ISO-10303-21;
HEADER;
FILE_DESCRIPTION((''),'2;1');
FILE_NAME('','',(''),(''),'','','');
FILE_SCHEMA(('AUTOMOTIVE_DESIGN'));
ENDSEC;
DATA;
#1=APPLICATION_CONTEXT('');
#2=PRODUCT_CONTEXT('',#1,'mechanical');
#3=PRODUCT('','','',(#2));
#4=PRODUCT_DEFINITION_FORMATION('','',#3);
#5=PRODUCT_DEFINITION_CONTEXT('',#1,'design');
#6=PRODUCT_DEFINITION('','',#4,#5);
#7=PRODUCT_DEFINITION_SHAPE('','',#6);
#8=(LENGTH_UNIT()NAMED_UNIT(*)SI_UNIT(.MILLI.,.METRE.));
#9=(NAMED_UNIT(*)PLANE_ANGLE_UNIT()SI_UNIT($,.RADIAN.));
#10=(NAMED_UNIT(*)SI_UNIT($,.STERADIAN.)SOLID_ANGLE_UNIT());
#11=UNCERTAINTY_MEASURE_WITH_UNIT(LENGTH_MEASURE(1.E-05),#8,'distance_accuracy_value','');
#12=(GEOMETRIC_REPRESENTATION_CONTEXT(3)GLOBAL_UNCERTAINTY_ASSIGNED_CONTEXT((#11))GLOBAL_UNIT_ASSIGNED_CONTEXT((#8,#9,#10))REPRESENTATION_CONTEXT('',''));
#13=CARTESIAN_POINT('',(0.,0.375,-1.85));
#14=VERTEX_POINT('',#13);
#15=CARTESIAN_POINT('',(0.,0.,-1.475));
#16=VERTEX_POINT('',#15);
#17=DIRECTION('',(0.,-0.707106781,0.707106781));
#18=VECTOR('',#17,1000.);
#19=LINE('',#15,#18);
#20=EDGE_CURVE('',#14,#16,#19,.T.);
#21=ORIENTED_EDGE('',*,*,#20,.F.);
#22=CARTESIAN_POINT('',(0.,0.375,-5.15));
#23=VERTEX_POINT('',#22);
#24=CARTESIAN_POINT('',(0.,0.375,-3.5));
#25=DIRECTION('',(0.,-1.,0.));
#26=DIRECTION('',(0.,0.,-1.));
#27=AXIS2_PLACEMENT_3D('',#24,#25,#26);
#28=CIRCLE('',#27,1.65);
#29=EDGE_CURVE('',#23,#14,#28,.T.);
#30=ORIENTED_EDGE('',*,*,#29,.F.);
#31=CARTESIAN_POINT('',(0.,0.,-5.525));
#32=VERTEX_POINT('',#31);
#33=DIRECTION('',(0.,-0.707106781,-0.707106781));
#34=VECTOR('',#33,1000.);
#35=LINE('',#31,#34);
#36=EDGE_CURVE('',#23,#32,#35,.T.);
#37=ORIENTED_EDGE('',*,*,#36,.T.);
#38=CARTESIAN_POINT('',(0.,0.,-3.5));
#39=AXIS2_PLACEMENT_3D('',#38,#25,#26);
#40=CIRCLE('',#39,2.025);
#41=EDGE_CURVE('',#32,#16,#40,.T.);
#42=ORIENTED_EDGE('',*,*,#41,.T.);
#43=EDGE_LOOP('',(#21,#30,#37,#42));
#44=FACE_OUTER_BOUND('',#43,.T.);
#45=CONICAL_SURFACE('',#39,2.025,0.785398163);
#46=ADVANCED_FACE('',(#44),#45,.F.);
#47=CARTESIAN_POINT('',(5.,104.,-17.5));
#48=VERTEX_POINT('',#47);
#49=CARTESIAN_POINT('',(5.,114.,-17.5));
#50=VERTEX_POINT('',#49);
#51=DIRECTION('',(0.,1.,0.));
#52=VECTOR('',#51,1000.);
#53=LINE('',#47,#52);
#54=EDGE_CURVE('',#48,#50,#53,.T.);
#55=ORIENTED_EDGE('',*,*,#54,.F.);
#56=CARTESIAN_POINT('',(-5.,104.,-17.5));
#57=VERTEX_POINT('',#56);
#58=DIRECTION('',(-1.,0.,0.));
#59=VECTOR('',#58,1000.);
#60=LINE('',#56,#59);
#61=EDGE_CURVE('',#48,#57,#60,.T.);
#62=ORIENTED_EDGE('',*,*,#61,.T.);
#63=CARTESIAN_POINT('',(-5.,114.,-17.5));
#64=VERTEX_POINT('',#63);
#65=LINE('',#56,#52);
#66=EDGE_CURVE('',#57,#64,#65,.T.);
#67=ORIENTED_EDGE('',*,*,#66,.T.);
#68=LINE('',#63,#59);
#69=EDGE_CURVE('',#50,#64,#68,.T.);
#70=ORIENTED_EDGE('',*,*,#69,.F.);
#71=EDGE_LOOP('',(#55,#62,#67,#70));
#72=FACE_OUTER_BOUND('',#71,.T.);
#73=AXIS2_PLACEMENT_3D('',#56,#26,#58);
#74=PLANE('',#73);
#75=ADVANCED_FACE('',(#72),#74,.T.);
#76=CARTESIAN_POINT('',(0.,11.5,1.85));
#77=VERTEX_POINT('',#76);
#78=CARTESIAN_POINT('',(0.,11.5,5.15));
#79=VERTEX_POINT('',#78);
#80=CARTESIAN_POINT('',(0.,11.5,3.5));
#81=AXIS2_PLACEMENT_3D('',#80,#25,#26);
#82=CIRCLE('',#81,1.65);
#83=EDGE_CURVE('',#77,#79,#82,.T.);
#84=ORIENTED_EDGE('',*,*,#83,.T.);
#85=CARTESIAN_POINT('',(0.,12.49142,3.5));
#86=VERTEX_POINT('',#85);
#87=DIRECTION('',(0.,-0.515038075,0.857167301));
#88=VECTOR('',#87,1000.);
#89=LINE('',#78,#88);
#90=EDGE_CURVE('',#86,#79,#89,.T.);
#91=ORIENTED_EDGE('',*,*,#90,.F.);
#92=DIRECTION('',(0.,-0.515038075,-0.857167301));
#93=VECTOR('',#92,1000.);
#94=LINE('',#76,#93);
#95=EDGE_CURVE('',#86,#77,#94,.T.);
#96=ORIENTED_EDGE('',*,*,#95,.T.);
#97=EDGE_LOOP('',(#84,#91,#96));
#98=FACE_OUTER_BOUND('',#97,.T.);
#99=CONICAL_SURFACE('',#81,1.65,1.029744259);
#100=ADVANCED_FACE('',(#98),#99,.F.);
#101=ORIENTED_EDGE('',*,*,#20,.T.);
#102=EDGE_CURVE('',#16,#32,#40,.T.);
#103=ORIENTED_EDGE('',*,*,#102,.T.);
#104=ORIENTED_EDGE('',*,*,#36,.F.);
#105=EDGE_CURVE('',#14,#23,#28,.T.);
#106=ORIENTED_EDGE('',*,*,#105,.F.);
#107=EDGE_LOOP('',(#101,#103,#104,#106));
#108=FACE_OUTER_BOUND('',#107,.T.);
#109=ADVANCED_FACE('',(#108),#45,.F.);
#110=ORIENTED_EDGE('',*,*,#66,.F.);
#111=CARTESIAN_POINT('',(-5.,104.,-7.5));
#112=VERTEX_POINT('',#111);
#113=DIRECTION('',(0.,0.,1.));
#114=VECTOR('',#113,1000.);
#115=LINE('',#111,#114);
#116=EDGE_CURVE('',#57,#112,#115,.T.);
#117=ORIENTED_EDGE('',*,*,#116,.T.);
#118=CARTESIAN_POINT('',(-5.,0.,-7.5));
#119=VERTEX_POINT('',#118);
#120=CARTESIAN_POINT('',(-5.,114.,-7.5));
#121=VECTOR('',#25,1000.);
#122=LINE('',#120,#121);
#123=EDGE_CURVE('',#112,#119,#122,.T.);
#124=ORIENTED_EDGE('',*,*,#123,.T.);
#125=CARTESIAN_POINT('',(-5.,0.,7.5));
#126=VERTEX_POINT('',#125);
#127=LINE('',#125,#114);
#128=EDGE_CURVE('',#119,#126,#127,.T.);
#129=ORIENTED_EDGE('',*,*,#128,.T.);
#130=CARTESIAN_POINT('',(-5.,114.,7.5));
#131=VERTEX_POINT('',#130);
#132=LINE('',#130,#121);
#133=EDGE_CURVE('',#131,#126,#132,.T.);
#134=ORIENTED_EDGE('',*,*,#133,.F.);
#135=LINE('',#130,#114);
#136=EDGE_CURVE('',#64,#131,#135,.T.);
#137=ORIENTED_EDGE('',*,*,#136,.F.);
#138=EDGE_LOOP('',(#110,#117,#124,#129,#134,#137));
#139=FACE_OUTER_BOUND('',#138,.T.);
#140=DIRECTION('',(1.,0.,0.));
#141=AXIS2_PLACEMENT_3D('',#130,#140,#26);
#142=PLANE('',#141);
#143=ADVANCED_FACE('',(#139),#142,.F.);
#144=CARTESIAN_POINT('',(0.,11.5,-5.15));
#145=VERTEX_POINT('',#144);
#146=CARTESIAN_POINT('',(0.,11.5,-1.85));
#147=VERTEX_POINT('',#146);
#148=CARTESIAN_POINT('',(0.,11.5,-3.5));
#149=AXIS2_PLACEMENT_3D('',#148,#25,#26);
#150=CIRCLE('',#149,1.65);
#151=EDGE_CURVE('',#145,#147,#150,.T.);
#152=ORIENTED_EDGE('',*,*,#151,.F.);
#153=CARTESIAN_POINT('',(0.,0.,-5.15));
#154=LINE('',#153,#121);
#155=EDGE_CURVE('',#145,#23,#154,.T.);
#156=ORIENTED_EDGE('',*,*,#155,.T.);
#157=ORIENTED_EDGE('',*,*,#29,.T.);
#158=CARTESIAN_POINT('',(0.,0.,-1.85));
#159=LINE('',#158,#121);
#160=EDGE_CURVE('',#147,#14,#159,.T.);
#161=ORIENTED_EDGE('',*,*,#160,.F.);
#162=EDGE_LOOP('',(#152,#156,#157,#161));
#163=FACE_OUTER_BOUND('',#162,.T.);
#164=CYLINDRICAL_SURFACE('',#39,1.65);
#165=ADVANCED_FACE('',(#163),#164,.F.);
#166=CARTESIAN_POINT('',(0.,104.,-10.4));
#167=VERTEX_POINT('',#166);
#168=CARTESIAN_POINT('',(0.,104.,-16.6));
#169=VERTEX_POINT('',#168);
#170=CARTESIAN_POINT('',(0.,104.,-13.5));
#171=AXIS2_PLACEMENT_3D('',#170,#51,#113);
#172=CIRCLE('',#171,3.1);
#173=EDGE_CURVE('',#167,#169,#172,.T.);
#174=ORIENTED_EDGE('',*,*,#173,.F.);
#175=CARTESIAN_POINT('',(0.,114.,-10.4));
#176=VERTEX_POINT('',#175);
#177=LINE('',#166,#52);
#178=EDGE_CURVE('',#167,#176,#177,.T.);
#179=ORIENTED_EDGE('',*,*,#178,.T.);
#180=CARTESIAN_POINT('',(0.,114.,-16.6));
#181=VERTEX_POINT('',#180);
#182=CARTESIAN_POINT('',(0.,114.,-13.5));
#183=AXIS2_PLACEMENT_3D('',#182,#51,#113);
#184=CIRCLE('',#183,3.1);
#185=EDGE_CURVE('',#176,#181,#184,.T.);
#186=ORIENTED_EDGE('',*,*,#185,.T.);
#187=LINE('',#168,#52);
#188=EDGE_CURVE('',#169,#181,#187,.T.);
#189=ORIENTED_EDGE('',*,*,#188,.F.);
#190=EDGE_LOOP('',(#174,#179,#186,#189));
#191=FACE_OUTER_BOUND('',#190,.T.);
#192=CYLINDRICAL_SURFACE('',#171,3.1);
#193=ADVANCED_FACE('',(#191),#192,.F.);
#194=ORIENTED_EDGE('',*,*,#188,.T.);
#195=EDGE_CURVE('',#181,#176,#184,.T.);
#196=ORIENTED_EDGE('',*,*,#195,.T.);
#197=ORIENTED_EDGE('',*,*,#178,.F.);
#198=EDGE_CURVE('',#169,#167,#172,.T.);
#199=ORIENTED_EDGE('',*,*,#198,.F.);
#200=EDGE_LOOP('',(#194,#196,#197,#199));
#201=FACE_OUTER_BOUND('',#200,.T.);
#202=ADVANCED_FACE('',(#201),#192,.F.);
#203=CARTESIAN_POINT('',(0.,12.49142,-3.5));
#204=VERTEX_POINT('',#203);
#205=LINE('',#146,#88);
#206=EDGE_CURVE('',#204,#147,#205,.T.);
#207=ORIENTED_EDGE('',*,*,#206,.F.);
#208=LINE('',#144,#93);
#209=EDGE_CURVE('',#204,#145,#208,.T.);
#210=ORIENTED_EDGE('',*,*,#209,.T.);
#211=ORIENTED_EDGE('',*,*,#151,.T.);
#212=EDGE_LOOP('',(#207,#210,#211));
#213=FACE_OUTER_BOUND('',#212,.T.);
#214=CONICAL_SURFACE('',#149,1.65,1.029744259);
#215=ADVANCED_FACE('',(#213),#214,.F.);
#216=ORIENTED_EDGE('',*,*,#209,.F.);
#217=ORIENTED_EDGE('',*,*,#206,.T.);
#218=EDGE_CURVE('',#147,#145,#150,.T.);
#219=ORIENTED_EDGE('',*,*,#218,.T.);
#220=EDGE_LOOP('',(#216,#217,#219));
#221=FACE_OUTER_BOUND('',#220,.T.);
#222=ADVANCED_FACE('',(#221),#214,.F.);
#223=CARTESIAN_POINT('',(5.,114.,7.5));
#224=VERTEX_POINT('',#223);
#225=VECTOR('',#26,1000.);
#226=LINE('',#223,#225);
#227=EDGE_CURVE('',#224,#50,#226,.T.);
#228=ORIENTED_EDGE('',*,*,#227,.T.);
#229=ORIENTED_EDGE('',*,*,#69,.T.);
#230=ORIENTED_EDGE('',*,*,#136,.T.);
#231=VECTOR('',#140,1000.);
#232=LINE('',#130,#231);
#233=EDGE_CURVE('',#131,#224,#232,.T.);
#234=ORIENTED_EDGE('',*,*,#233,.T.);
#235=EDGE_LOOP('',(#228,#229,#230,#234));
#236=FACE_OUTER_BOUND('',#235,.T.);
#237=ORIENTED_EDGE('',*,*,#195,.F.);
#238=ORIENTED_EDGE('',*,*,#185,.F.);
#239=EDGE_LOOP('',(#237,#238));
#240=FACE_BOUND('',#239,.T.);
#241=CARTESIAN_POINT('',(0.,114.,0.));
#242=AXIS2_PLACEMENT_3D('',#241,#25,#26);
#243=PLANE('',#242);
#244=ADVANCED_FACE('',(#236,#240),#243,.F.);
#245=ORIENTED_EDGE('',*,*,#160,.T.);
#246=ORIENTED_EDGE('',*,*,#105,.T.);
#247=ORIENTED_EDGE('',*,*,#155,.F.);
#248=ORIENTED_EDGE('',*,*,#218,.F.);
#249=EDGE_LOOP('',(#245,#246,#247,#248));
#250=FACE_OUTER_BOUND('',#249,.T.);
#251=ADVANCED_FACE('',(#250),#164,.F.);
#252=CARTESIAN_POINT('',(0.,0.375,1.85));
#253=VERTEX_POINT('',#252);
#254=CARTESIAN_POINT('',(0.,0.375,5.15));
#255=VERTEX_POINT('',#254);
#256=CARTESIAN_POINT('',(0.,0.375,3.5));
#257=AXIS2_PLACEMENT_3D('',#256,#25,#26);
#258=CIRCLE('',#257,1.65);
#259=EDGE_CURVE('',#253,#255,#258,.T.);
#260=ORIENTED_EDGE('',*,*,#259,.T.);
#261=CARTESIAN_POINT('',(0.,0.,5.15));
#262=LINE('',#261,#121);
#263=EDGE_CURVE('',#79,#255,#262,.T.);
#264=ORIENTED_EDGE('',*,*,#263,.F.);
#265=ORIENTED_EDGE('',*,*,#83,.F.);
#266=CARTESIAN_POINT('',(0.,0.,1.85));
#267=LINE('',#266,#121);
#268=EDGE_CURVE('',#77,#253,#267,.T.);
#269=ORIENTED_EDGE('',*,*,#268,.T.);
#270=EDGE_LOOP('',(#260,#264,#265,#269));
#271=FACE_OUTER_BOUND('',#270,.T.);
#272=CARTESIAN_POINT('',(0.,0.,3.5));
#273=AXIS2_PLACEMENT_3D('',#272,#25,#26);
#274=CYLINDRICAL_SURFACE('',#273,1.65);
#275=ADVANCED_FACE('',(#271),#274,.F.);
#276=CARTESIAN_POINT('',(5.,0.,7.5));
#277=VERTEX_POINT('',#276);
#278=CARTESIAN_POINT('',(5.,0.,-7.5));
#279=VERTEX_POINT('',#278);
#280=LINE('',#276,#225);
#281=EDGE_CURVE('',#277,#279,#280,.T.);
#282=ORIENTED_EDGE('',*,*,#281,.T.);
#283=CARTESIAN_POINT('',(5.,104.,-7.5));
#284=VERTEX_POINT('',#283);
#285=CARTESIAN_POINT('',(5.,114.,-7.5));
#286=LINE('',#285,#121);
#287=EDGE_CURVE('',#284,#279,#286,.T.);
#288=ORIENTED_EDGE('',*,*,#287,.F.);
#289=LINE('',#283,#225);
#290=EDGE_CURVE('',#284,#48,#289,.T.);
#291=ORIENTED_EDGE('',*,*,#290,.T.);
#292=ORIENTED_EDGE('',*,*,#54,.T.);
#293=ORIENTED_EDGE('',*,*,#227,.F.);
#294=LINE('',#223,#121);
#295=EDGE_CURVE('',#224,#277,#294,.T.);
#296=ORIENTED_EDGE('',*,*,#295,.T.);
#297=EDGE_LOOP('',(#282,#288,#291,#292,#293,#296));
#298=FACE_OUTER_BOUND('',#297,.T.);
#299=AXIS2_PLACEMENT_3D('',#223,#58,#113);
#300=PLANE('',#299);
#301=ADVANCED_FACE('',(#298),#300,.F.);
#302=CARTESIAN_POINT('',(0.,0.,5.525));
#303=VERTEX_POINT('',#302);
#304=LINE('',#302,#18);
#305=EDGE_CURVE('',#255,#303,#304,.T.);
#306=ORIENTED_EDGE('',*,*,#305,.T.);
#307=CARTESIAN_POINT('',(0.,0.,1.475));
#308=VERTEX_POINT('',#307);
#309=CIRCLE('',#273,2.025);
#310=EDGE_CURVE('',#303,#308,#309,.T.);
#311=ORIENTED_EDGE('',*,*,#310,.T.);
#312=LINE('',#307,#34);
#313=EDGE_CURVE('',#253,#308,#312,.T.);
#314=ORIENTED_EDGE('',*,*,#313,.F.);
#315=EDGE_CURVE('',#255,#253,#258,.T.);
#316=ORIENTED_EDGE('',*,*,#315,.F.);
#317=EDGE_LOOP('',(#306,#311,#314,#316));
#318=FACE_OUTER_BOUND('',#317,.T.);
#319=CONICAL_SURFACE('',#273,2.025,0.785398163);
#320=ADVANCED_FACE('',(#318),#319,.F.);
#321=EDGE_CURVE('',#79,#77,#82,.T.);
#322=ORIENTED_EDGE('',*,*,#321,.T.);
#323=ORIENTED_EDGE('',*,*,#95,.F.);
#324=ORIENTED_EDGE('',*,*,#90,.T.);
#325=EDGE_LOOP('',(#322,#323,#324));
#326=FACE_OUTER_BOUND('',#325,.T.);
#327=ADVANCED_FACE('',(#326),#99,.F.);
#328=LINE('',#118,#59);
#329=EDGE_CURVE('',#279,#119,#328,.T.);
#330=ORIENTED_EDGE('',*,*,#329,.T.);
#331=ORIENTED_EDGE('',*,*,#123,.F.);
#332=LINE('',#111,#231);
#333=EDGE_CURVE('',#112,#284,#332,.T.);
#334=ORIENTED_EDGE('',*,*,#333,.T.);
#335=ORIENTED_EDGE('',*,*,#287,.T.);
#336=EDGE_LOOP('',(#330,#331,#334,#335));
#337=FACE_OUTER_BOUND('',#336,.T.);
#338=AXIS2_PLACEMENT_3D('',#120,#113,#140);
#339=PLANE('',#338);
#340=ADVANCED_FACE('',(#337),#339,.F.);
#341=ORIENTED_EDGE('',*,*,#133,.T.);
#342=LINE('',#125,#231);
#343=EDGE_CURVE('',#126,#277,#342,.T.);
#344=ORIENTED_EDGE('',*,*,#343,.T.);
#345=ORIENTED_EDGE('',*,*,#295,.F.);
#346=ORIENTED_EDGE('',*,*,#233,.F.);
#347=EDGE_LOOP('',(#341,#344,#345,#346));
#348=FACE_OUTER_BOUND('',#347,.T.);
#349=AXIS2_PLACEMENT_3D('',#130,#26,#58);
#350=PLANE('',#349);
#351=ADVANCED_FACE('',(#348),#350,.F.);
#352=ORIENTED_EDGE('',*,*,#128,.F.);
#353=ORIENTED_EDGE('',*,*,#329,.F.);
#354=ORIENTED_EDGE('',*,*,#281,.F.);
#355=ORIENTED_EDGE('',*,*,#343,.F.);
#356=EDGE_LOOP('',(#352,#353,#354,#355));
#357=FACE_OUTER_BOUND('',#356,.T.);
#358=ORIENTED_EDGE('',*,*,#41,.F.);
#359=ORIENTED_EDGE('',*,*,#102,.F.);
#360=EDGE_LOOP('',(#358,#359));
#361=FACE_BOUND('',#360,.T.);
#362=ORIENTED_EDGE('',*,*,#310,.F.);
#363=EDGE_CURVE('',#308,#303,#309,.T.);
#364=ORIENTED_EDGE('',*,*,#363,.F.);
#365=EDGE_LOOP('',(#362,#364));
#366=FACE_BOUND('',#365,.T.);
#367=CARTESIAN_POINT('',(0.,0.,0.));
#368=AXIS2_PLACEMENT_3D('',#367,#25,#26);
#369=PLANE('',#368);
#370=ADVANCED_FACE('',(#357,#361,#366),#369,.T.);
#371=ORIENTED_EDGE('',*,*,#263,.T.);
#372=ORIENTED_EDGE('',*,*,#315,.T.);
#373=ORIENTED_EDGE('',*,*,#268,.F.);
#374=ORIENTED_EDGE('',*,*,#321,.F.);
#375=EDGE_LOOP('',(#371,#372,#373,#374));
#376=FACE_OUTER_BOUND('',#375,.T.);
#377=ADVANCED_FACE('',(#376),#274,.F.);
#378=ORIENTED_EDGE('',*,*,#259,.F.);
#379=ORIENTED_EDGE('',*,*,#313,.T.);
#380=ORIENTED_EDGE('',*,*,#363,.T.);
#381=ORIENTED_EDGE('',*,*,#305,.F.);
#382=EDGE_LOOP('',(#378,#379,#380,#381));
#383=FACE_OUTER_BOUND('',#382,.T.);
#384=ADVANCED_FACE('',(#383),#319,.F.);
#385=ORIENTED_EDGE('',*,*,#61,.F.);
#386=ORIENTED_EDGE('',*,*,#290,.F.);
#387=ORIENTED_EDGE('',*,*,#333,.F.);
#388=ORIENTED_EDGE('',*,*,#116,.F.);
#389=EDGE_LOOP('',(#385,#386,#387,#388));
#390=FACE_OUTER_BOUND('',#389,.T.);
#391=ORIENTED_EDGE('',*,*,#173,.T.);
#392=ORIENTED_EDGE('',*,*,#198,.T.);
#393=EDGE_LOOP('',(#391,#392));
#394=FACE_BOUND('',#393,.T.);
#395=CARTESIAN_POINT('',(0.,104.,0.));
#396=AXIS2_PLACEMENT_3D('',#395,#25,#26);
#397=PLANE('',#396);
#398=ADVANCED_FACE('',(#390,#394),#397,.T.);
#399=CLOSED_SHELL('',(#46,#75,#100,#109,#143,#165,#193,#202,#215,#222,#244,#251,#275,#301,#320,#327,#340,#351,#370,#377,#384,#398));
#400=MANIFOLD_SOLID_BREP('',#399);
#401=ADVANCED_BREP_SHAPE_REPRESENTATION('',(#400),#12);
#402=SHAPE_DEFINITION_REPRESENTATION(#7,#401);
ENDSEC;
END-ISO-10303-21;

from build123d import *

# Parameters (mm, degrees)
SKETCH1_W                   = 10
SKETCH1_H                   = 15
BOSS_EXTRUDE1_DEPTH         = 114
SKETCH2_W                   = 10
SKETCH2_H                   = 10
SKETCH2_R                   = 3.1
BOSS_EXTRUDE2_DEPTH         = 10
M4_TAPPED_HOLE1_D           = 3.3
M4_TAPPED_HOLE1_DEPTH       = 11.5
M4_TAPPED_HOLE1_CSINK_D     = 4.05
M4_TAPPED_HOLE1_CSINK_ANGLE = 90
M4_TAPPED_HOLE1_TIP         = 0.991420021


with BuildPart() as part:
    # Sketch1 → Boss-Extrude1 (new body)
    with BuildSketch(Plane(origin=(0, 0, 0), x_dir=(1, 0, 0), z_dir=(0, 1, 0))):
        Rectangle(SKETCH1_W, SKETCH1_H)
    extrude(amount=BOSS_EXTRUDE1_DEPTH)

    # Sketch2 → Boss-Extrude2 (add)
    with BuildSketch(Plane(origin=(0, 114, 0), x_dir=(1, 0, 0), z_dir=(0, 1, 0))):
        with Locations((0, 12.5)):
            Rectangle(SKETCH2_W, SKETCH2_H)
        with Locations(Location((0, 13.5, 0), (0, 0, 270))):
            Circle(SKETCH2_R, mode=Mode.SUBTRACT)
    extrude(amount=-BOSS_EXTRUDE2_DEPTH)

    # M4 Tapped Hole1
    with Locations(Plane(origin=(0, 0, 0), x_dir=(-1, 0, 0), z_dir=(0, -1, 0))):
        with Locations((0, 3.5), (0, -3.5)):
            CounterSinkHole(M4_TAPPED_HOLE1_D / 2, M4_TAPPED_HOLE1_CSINK_D / 2, depth=M4_TAPPED_HOLE1_DEPTH, counter_sink_angle=M4_TAPPED_HOLE1_CSINK_ANGLE)
            with Locations((0, 0, -(M4_TAPPED_HOLE1_DEPTH + M4_TAPPED_HOLE1_TIP / 2))):  # 118° drill point
                Cone(0, M4_TAPPED_HOLE1_D / 2, M4_TAPPED_HOLE1_TIP, mode=Mode.SUBTRACT)


solid = part.part
